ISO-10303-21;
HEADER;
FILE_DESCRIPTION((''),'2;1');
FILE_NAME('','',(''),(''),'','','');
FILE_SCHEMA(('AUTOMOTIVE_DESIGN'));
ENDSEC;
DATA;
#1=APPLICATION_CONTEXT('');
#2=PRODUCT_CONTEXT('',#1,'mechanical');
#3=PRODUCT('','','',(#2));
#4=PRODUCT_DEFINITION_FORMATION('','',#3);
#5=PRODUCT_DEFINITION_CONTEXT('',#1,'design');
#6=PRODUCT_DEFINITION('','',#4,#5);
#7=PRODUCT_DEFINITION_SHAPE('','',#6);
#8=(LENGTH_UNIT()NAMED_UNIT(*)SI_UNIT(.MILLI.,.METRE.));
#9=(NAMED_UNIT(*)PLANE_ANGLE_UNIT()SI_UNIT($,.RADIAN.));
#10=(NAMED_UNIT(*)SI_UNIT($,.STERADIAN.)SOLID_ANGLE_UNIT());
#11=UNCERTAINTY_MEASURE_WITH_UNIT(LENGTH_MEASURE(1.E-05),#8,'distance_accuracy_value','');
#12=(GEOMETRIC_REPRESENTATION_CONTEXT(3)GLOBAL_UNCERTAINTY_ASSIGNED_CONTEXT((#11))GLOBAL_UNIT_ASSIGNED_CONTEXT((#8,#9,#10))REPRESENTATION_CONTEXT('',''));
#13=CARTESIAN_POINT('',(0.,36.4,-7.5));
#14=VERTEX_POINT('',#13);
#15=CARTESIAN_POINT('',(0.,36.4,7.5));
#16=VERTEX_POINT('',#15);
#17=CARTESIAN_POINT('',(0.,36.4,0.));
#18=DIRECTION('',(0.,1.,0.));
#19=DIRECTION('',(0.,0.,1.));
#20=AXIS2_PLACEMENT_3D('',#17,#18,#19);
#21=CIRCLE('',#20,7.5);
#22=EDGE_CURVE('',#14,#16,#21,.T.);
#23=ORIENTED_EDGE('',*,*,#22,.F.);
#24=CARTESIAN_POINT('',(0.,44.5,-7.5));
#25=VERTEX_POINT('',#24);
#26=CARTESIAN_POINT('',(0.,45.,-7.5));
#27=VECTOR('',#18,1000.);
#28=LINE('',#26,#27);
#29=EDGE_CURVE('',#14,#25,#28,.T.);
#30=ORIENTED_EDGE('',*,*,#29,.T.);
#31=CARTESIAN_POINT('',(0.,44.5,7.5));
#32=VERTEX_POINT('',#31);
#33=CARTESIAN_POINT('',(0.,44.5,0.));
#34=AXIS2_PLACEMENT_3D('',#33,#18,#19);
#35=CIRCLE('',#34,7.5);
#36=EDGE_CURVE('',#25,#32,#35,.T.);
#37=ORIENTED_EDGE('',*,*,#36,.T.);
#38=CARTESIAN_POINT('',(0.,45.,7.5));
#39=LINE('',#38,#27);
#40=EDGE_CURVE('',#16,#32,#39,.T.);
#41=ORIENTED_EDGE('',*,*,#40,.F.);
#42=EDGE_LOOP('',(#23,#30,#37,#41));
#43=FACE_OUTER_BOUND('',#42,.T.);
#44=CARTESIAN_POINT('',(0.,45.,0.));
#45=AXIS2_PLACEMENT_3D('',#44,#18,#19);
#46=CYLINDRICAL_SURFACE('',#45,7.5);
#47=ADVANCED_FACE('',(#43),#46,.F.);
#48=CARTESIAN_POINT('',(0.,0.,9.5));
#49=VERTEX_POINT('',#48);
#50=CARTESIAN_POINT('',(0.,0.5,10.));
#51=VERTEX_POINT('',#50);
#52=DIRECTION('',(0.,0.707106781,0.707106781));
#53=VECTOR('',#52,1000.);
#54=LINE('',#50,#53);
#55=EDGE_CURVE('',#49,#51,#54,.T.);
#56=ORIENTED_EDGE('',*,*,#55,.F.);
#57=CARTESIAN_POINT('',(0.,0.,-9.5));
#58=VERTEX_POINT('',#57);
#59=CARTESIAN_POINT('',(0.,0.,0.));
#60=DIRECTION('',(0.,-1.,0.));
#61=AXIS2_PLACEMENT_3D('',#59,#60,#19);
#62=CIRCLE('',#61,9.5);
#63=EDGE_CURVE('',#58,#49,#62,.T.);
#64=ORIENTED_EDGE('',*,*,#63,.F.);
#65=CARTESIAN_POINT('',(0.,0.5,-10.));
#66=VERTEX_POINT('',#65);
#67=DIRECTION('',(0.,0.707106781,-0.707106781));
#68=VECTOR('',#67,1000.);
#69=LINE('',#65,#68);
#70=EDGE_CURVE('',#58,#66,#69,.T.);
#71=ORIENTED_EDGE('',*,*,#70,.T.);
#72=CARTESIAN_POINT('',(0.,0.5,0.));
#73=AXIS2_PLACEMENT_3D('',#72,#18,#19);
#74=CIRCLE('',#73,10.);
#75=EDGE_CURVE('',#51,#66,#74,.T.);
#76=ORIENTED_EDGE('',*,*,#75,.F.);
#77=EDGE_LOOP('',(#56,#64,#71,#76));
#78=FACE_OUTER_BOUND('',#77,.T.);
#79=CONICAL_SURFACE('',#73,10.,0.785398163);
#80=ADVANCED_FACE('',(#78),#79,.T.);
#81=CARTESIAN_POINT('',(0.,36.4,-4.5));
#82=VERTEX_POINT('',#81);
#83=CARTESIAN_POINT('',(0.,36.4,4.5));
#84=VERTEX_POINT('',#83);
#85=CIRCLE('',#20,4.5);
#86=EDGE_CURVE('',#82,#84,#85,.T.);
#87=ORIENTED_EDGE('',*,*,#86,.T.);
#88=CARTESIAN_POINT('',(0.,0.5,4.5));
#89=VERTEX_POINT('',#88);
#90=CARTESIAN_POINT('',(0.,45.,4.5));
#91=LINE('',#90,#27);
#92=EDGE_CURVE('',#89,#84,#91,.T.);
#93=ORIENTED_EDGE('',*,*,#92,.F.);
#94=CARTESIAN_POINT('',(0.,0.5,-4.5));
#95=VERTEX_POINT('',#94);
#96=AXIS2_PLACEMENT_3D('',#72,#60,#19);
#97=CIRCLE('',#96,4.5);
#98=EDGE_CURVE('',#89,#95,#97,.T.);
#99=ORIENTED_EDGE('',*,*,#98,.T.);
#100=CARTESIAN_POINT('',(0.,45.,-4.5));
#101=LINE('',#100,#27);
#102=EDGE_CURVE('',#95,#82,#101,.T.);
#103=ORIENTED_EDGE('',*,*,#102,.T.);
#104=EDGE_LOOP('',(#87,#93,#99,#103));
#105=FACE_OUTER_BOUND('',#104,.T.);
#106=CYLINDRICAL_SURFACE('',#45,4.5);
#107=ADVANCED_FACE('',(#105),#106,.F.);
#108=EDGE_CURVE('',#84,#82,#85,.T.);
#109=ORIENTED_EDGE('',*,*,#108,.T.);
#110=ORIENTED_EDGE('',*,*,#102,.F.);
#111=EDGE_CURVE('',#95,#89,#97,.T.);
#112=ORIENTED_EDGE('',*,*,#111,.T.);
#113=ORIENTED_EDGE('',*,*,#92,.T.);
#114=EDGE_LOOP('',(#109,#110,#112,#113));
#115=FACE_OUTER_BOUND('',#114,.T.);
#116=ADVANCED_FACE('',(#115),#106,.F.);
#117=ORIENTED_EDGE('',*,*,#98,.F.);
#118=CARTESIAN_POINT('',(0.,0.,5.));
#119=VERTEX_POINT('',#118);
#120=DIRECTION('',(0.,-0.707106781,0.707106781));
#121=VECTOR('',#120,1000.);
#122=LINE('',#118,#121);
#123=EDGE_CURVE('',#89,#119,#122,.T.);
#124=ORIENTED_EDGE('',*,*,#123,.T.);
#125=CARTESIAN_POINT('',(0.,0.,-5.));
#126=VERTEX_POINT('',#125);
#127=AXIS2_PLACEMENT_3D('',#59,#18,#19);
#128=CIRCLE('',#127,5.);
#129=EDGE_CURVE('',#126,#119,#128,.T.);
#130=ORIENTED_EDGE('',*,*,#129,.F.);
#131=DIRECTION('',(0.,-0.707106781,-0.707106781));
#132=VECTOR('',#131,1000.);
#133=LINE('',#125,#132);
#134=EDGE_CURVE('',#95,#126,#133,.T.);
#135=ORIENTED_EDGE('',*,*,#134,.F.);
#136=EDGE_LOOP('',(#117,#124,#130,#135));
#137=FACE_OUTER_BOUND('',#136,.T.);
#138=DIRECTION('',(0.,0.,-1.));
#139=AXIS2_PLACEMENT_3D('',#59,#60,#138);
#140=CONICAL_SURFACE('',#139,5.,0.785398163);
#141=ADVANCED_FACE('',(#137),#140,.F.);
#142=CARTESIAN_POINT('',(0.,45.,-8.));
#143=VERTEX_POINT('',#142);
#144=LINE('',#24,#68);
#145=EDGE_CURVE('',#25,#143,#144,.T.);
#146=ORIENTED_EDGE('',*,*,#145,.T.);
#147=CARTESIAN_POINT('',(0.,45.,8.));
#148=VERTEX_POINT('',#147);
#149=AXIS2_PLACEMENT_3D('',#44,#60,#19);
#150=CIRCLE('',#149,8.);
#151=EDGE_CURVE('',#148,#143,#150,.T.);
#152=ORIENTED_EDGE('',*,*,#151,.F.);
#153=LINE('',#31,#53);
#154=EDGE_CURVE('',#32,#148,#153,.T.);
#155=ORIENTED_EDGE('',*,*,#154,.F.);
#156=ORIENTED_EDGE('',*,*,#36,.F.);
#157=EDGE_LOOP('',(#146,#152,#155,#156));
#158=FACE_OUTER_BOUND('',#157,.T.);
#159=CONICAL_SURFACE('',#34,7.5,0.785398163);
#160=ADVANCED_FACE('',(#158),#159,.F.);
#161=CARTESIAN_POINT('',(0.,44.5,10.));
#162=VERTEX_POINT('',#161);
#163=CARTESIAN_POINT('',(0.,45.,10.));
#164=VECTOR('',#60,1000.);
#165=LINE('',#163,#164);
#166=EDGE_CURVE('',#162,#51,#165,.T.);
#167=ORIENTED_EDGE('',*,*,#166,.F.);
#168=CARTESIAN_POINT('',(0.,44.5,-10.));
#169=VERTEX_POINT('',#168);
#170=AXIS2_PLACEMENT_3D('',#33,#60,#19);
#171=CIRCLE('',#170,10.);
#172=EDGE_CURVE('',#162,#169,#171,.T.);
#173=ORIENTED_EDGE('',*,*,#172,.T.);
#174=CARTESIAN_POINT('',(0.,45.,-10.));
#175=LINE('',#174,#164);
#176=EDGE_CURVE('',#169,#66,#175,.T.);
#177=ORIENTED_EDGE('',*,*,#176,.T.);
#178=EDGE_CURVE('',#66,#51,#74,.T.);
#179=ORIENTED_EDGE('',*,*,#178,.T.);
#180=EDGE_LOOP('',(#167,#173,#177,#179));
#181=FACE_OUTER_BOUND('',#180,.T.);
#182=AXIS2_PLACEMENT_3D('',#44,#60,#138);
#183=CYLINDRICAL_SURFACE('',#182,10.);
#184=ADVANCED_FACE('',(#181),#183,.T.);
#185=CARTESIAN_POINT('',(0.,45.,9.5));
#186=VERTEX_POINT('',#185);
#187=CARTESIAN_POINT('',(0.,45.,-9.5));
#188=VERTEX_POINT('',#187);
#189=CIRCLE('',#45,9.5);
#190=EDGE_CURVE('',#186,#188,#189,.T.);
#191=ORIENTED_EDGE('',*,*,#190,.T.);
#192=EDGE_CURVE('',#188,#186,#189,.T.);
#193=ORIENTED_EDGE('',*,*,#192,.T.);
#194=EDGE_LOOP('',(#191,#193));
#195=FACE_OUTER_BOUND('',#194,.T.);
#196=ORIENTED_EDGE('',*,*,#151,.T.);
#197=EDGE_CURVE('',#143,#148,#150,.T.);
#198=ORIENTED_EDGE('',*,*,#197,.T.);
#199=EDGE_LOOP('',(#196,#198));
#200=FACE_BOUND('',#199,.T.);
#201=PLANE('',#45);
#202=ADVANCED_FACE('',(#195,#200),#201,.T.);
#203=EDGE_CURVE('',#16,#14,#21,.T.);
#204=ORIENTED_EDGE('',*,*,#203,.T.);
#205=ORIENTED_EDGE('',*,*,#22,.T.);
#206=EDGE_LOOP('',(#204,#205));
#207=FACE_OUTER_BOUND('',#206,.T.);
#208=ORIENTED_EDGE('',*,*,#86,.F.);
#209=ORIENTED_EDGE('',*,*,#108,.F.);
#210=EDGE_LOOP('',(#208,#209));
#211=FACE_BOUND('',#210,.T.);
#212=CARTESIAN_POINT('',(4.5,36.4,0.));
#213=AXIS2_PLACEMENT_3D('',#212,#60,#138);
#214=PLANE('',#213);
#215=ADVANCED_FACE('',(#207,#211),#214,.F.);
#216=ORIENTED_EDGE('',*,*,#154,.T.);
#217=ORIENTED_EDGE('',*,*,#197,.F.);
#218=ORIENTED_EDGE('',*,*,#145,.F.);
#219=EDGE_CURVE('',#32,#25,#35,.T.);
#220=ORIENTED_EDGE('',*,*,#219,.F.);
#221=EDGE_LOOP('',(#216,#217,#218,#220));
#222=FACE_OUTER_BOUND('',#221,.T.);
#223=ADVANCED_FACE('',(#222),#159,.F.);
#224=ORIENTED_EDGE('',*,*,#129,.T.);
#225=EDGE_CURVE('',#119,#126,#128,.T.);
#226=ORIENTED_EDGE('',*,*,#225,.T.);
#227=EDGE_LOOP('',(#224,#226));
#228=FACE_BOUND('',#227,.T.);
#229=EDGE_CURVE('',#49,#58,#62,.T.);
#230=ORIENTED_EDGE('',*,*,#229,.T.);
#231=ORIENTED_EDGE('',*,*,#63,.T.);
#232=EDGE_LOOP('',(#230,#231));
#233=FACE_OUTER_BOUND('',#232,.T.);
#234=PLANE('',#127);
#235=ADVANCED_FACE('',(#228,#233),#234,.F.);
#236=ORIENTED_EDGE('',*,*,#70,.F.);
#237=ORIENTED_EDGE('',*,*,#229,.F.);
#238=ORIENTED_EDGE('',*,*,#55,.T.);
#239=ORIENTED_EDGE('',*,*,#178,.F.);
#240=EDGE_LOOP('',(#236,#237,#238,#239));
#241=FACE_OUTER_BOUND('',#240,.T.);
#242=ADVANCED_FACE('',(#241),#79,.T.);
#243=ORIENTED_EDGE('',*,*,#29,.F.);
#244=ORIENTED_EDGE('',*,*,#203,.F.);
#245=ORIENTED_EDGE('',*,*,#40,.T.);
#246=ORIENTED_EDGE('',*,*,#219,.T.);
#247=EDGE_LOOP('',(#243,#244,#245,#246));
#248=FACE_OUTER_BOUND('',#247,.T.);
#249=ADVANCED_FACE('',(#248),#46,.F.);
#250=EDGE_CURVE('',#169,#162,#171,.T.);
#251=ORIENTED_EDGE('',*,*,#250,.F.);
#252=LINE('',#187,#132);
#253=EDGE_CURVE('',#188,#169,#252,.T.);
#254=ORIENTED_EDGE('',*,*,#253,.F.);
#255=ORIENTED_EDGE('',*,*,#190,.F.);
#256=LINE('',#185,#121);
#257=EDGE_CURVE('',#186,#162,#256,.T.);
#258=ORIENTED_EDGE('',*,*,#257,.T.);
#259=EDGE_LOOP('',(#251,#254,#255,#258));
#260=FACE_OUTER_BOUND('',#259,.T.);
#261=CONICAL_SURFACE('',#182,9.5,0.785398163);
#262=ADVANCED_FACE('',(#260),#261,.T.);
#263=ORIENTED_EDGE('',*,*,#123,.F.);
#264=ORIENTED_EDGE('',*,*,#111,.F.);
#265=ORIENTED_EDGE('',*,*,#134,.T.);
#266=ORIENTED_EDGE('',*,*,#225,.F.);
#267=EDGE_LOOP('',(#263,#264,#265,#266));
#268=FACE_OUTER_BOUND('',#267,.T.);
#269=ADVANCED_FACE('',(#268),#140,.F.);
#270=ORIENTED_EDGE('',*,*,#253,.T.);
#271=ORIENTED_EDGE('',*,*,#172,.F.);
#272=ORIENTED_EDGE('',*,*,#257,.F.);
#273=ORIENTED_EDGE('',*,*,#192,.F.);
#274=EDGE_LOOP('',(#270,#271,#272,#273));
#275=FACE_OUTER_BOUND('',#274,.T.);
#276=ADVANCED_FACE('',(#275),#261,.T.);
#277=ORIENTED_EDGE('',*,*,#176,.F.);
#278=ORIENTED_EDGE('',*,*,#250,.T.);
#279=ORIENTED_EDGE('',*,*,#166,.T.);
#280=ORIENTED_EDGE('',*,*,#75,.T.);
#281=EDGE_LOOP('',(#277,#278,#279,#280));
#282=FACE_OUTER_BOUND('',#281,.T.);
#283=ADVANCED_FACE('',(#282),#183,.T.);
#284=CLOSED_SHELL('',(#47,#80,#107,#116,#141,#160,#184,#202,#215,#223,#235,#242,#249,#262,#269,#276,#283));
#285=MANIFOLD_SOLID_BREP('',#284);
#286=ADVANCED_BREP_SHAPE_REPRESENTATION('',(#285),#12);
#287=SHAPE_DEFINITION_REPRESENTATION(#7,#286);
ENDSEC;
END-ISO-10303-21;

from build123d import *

# Parameters (mm, degrees)
SKETCH1_R                                           = 10
BOSS_EXTRUDE1_DEPTH                                 = 45
CBORE_FOR_M8_HEX_SOCKET_HEAD_CAP_SCREW1_D           = 9
CBORE_FOR_M8_HEX_SOCKET_HEAD_CAP_SCREW1_CBORE_D     = 15
CBORE_FOR_M8_HEX_SOCKET_HEAD_CAP_SCREW1_CBORE_DEPTH = 8.6
CHAMFER1_SIZE                                       = 0.5


with BuildPart() as part:
    # Sketch1 → Boss-Extrude1 (new body)
    with BuildSketch(Plane(origin=(0, 0, 0), x_dir=(1, 0, 0), z_dir=(0, 1, 0))):
        with Locations(Location((0, 0, 0), (0, 0, 90))):
            Circle(SKETCH1_R)
    extrude(amount=BOSS_EXTRUDE1_DEPTH)

    # CBORE for M8 Hex Socket Head Cap Screw1 (through all)
    with Locations(Plane(origin=(0, 45, 0), x_dir=(1, 0, 0), z_dir=(0, 1, 0))):
        with Locations((0, 0)):
            CounterBoreHole(CBORE_FOR_M8_HEX_SOCKET_HEAD_CAP_SCREW1_D / 2, CBORE_FOR_M8_HEX_SOCKET_HEAD_CAP_SCREW1_CBORE_D / 2, CBORE_FOR_M8_HEX_SOCKET_HEAD_CAP_SCREW1_CBORE_DEPTH)

    # Chamfer1
    chamfer1_edges = [part.edges().sort_by_distance(p)[0] for p in [
        (0, 0, 10),
        (0, 45, 10),
        (-7.5, 45, 0),
        (4.5, 0, 0),
    ]]
    chamfer(chamfer1_edges, length=CHAMFER1_SIZE)


solid = part.part
